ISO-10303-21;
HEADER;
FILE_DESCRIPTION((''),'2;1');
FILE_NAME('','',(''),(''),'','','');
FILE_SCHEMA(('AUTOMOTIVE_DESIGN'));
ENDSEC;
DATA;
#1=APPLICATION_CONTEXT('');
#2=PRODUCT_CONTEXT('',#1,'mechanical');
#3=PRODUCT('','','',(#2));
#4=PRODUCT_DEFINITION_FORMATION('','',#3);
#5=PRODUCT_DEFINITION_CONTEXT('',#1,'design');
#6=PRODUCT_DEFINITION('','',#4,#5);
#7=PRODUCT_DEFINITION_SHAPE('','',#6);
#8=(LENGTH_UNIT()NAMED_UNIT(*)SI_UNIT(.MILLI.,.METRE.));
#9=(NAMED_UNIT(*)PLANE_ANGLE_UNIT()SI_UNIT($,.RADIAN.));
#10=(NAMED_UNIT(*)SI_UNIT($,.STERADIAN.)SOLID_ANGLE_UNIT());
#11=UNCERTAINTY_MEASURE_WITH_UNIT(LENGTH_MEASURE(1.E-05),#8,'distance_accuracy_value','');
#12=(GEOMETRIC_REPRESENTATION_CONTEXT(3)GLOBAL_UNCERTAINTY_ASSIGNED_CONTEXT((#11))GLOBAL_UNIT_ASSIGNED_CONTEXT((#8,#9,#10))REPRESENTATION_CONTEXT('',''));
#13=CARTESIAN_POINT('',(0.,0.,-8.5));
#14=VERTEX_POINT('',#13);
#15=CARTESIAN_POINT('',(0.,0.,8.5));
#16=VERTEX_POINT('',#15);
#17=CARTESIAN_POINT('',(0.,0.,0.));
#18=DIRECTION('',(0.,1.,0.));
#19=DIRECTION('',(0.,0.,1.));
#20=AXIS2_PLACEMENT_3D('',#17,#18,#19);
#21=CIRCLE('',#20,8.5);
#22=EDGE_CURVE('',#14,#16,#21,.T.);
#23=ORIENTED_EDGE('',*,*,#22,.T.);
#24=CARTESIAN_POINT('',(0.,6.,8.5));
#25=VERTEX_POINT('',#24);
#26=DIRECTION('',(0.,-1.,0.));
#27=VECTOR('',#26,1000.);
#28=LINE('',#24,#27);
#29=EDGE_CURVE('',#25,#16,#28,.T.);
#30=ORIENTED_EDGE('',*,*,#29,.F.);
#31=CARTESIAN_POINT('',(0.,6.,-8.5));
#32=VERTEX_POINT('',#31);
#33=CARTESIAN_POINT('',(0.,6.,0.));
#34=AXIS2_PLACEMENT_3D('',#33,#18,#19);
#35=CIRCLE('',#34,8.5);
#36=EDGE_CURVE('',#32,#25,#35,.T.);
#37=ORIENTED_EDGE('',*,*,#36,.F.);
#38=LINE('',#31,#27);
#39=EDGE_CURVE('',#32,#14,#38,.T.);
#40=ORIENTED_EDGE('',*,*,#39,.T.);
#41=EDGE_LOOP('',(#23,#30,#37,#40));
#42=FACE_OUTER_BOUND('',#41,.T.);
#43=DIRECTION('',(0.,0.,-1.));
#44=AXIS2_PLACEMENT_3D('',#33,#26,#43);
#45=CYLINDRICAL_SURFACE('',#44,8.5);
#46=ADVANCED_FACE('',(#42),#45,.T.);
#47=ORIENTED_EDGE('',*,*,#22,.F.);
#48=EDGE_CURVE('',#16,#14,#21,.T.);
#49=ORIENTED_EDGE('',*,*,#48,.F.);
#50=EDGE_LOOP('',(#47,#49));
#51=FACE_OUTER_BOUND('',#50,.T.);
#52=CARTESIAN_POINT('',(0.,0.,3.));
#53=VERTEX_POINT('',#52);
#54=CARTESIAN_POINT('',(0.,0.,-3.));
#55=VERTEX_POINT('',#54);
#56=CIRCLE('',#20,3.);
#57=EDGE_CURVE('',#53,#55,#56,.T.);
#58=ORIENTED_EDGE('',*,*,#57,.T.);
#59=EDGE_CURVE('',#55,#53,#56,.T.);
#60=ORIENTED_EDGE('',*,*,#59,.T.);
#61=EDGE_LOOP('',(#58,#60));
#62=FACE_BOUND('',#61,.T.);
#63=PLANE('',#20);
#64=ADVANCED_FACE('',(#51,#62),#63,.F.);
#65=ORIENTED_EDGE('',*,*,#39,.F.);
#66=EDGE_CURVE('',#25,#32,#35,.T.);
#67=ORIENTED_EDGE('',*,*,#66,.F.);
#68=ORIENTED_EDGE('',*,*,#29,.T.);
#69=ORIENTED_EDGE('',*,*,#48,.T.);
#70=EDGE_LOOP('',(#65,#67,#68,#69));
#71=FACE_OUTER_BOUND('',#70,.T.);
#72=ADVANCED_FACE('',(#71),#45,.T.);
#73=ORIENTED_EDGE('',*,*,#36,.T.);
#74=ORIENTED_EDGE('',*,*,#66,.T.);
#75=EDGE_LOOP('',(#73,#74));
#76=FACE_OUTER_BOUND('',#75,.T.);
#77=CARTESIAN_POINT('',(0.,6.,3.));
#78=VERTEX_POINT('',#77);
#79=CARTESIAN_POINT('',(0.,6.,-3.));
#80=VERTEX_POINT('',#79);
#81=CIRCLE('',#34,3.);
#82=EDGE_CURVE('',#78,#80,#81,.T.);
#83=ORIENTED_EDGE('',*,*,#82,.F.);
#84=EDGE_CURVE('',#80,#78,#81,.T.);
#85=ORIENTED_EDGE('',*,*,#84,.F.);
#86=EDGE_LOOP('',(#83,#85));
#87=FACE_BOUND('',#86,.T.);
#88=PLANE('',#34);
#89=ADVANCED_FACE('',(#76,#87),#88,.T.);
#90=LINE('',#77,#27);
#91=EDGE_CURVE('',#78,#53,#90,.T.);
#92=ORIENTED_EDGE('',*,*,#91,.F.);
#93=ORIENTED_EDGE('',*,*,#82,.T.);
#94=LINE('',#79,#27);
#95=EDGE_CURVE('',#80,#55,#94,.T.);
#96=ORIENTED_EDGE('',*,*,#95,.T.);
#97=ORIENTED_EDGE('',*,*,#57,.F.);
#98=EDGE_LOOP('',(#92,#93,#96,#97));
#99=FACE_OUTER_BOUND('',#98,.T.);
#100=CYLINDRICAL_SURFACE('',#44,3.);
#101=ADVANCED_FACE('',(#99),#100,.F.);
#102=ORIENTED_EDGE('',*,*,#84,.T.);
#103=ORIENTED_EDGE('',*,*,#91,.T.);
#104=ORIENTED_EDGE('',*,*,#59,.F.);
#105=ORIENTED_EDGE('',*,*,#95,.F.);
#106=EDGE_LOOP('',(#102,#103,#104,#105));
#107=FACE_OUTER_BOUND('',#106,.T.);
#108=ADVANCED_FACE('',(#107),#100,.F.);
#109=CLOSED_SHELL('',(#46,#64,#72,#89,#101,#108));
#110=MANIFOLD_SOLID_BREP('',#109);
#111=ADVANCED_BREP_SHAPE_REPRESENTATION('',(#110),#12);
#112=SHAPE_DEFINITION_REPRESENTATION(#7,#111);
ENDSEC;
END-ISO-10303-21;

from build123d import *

# Parameters (mm, degrees)
SKETCH1_R           = 8.5
SKETCH1_R_2         = 3
BOSS_EXTRUDE1_DEPTH = 6


with BuildPart() as part:
    # Sketch1 → Boss-Extrude1 (new body)
    with BuildSketch(Plane(origin=(0, 0, 0), x_dir=(1, 0, 0), z_dir=(0, 1, 0))):
        with Locations(Location((0, 0, 0), (0, 0, 270))):
            Circle(SKETCH1_R)
        with Locations(Location((0, 0, 0), (0, 0, 270))):
            Circle(SKETCH1_R_2, mode=Mode.SUBTRACT)
    extrude(amount=BOSS_EXTRUDE1_DEPTH)


solid = part.part
